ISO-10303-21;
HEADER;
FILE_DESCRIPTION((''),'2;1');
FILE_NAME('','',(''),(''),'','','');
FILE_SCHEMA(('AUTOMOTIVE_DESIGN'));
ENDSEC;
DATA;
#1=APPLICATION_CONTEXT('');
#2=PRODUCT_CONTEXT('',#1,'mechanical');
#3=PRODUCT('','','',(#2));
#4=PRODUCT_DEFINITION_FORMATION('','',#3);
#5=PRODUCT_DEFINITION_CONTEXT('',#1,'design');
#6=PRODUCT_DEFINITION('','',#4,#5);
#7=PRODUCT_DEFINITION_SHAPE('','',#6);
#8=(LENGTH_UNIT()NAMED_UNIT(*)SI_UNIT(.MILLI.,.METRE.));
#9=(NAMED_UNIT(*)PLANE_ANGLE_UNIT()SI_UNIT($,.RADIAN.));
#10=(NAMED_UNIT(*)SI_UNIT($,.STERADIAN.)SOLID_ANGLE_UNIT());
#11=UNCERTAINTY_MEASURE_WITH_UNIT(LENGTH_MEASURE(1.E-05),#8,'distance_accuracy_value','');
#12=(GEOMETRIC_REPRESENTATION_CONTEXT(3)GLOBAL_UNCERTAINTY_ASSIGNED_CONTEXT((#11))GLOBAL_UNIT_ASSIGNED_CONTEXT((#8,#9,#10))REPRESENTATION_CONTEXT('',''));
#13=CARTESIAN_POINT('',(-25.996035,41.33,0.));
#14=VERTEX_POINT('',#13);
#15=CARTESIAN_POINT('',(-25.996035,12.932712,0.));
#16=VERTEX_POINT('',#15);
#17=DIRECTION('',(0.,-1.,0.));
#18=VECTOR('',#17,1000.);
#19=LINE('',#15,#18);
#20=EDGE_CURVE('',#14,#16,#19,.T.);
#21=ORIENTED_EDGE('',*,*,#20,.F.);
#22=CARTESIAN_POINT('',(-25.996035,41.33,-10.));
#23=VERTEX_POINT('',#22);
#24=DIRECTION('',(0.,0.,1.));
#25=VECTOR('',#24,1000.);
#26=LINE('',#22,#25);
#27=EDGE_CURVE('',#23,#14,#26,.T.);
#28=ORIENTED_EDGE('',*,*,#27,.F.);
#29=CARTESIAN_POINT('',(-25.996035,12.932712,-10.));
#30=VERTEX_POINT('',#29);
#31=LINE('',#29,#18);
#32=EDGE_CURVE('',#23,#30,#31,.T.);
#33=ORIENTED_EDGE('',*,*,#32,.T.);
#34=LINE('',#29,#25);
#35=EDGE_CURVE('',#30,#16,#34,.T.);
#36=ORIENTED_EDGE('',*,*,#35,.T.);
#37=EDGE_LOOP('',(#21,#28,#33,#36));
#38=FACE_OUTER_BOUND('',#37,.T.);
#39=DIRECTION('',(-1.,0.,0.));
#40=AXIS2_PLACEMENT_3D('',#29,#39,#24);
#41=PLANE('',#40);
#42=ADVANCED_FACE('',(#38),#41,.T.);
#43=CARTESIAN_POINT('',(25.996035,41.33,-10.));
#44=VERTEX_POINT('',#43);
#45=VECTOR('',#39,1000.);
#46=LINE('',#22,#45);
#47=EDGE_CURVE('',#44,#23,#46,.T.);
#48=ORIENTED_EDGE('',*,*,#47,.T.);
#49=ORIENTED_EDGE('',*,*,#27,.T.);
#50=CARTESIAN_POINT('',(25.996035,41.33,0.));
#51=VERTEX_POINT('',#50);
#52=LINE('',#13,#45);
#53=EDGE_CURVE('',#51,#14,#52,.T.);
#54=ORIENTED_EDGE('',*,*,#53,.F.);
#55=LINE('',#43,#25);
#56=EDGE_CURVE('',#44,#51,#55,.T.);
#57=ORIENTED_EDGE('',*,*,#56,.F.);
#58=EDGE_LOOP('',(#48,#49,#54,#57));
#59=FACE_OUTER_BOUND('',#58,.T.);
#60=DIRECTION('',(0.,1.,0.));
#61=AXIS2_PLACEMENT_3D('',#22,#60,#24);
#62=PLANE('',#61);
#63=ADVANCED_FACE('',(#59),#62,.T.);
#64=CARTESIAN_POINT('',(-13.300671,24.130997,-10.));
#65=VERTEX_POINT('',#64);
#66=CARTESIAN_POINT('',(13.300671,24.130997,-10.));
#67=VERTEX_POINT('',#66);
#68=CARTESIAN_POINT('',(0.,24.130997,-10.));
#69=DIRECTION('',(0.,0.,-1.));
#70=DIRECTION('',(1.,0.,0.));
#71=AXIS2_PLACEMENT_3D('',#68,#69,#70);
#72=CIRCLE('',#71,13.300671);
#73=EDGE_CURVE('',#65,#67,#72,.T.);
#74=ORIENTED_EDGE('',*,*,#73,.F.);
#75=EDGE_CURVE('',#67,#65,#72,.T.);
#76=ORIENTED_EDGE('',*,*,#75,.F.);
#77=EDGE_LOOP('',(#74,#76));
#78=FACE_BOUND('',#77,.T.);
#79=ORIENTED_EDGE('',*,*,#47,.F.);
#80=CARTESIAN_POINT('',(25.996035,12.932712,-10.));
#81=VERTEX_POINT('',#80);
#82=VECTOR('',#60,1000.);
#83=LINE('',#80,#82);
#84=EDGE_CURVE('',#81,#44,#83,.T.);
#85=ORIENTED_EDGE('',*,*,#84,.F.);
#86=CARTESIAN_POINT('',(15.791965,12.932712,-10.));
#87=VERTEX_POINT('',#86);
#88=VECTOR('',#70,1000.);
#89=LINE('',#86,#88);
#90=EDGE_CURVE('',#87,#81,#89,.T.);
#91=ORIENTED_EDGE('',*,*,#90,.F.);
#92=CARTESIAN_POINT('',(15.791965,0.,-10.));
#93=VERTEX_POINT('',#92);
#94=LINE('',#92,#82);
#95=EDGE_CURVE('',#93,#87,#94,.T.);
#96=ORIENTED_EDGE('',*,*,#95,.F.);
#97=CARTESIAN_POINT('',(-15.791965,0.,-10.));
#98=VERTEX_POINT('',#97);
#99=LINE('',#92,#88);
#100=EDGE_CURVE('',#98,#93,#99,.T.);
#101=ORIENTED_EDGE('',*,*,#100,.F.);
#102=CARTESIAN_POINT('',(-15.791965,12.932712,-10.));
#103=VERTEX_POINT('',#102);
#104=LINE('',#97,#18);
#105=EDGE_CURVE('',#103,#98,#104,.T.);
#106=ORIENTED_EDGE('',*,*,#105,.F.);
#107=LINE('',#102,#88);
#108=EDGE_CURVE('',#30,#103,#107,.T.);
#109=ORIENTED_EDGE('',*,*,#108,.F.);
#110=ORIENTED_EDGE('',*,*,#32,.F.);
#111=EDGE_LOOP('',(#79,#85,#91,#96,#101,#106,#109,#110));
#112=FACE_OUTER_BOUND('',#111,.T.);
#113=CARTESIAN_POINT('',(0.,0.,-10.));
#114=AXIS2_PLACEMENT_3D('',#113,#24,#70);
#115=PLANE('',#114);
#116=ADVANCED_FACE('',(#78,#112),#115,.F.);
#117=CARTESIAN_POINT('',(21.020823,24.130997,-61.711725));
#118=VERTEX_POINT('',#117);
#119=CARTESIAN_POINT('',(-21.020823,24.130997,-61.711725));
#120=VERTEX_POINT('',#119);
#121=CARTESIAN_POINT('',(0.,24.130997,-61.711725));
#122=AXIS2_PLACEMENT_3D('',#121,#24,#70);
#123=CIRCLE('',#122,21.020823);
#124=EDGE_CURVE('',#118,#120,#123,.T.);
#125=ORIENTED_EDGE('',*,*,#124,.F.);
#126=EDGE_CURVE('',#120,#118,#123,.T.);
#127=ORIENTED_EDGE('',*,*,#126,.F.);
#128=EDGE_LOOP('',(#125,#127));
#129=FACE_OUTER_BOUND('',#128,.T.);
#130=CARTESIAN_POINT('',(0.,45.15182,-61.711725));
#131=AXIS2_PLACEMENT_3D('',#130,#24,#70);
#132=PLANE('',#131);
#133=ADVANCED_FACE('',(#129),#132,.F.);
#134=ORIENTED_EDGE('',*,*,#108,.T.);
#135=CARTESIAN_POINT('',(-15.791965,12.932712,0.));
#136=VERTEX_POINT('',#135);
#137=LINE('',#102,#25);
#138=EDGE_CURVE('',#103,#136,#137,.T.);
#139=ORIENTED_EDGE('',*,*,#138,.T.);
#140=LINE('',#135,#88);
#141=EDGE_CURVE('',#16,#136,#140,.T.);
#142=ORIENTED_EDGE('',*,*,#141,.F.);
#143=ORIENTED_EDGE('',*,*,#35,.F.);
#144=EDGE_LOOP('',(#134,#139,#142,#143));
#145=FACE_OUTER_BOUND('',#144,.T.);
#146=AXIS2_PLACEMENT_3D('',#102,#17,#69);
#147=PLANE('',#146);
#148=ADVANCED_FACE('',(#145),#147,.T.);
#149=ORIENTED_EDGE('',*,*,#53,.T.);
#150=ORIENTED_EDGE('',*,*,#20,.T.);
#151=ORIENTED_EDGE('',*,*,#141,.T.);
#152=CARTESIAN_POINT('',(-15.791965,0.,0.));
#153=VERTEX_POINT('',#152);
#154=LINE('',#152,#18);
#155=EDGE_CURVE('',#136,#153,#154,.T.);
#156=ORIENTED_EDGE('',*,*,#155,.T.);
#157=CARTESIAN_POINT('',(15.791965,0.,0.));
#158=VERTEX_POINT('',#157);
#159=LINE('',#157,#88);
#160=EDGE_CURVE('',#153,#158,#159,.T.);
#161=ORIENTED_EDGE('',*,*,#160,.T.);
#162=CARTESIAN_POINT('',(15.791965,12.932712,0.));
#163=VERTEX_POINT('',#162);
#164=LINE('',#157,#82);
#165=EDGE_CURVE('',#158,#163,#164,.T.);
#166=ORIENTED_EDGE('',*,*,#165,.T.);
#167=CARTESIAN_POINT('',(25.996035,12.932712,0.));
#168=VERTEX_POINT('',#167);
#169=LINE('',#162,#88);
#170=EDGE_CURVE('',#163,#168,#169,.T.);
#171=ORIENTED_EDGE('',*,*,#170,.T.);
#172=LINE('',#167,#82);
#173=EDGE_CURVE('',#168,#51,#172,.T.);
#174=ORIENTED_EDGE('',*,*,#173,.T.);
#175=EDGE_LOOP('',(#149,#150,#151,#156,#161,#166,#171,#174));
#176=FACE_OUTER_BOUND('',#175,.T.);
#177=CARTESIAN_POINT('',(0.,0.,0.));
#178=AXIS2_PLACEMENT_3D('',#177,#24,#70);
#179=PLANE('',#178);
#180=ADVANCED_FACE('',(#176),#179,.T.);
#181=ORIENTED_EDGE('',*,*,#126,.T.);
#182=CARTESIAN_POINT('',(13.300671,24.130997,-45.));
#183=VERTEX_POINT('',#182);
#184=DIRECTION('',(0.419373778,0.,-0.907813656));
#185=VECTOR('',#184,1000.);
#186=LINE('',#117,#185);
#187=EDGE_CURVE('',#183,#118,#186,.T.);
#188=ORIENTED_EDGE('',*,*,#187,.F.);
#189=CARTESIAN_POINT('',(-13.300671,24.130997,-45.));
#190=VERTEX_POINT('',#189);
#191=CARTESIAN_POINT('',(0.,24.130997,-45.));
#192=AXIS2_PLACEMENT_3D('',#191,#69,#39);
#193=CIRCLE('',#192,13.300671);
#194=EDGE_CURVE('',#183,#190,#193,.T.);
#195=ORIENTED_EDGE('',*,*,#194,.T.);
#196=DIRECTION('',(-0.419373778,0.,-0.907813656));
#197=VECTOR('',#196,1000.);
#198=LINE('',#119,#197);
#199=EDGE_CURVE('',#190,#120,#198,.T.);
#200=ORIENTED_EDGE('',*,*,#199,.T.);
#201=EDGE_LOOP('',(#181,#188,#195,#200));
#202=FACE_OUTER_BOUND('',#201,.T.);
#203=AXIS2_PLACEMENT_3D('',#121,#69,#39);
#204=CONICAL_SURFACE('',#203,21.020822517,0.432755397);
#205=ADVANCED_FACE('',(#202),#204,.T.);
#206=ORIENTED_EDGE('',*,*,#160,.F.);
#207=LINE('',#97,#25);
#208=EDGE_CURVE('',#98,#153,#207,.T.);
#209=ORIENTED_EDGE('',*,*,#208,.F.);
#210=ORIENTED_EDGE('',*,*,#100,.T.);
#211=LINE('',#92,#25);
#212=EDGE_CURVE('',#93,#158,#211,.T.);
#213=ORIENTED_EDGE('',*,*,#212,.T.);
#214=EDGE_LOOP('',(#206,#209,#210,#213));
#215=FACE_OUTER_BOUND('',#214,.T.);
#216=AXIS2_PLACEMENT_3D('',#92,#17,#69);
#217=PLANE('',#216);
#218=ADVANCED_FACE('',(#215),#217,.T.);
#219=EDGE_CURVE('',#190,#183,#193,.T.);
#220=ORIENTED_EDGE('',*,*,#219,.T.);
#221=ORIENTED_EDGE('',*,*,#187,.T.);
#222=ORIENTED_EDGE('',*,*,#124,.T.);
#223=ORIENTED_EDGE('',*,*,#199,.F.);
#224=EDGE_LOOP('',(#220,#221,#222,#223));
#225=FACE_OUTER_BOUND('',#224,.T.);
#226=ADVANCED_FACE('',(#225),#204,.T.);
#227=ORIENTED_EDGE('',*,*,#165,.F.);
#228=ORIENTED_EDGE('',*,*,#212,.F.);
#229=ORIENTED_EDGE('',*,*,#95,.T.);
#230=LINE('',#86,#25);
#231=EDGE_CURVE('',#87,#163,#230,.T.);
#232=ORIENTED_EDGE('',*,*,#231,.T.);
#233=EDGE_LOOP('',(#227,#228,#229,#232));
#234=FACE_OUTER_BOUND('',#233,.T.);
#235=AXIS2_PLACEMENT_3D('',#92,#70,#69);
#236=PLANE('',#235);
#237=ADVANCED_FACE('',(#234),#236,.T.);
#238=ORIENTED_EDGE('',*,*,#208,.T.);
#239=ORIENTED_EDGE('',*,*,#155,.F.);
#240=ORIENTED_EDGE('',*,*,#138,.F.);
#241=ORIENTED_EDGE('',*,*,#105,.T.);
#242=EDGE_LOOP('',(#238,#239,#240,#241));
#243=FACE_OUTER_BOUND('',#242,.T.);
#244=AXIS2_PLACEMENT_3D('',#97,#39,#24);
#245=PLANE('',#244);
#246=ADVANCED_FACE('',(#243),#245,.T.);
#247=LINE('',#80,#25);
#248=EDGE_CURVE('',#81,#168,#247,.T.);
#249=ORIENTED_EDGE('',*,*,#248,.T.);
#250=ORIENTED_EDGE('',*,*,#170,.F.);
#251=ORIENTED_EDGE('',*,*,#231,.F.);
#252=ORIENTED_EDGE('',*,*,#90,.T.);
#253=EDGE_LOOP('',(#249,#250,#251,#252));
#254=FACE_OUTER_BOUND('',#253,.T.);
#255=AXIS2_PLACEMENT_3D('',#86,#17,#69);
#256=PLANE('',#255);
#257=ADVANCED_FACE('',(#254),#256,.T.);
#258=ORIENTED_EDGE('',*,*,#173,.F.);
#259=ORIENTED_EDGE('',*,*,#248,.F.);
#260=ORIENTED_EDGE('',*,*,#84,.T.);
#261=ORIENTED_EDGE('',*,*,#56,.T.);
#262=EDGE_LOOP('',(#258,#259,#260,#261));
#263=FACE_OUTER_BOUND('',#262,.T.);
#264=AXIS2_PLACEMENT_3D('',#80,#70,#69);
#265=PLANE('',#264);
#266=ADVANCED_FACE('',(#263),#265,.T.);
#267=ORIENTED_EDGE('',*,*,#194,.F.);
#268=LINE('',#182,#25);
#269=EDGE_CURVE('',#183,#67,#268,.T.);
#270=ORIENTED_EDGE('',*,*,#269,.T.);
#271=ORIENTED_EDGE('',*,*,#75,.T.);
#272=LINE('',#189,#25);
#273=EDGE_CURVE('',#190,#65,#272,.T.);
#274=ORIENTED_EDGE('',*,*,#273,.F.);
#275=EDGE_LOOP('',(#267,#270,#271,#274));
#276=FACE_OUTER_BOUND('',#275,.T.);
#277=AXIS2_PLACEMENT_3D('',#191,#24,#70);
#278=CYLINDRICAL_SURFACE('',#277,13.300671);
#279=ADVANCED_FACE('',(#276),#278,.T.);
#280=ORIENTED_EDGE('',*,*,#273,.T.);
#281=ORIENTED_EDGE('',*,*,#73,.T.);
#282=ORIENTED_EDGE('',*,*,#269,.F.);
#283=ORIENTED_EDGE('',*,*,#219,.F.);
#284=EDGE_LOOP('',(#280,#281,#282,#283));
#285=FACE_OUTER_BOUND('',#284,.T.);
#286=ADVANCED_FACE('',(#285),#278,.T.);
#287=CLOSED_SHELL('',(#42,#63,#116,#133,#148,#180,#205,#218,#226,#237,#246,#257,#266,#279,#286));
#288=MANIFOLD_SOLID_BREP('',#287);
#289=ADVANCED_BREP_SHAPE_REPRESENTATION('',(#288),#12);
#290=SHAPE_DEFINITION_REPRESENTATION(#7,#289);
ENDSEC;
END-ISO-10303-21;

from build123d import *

# Parameters (mm, degrees)
BOSS_EXTRUDE1_DEPTH = 10
SKETCH2_R           = 13.300670815
BOSS_EXTRUDE2_DEPTH = 35


with BuildPart() as part:
    # Sketch1 → Boss-Extrude1 (new body)
    with BuildSketch(Plane.XY):
        Polygon((15.791965236, 0), (-15.791965236, 0), (-15.791965236, 12.932711507), (-25.996035407, 12.932711507), (-25.996035407, 41.33), (25.996035407, 41.33), (25.996035407, 12.932711507), (15.791965236, 12.932711507), align=None)
    extrude(amount=-BOSS_EXTRUDE1_DEPTH)

    # Sketch2 → Boss-Extrude2 (add)
    with BuildSketch(Plane(origin=(0, 0, -10), x_dir=(-1, 0, 0), z_dir=(0, 0, -1))):
        with Locations(Location((0, 24.130997224, 0), (0, 0, 180))):
            Circle(SKETCH2_R)
    extrude(amount=BOSS_EXTRUDE2_DEPTH)

    # Sketch5 → Revolve4 (revolve)
    with BuildSketch(Plane(origin=(0, 0, 0), x_dir=(0, 0, -1), z_dir=(1, 0, 0)), mode=Mode.PRIVATE) as revolve4_sk:
        Polygon((45, 37.431668039), (61.711724745, 45.151819741), (61.711724745, 24.130997224), (45, 24.130997224), align=None)
    revolve(revolve4_sk.sketch.rotate(Axis((0, 24.130997224, -45), (0, 0, -1)), 90), axis=Axis((0, 24.130997224, -45), (0, 0, -1)))


solid = part.part
